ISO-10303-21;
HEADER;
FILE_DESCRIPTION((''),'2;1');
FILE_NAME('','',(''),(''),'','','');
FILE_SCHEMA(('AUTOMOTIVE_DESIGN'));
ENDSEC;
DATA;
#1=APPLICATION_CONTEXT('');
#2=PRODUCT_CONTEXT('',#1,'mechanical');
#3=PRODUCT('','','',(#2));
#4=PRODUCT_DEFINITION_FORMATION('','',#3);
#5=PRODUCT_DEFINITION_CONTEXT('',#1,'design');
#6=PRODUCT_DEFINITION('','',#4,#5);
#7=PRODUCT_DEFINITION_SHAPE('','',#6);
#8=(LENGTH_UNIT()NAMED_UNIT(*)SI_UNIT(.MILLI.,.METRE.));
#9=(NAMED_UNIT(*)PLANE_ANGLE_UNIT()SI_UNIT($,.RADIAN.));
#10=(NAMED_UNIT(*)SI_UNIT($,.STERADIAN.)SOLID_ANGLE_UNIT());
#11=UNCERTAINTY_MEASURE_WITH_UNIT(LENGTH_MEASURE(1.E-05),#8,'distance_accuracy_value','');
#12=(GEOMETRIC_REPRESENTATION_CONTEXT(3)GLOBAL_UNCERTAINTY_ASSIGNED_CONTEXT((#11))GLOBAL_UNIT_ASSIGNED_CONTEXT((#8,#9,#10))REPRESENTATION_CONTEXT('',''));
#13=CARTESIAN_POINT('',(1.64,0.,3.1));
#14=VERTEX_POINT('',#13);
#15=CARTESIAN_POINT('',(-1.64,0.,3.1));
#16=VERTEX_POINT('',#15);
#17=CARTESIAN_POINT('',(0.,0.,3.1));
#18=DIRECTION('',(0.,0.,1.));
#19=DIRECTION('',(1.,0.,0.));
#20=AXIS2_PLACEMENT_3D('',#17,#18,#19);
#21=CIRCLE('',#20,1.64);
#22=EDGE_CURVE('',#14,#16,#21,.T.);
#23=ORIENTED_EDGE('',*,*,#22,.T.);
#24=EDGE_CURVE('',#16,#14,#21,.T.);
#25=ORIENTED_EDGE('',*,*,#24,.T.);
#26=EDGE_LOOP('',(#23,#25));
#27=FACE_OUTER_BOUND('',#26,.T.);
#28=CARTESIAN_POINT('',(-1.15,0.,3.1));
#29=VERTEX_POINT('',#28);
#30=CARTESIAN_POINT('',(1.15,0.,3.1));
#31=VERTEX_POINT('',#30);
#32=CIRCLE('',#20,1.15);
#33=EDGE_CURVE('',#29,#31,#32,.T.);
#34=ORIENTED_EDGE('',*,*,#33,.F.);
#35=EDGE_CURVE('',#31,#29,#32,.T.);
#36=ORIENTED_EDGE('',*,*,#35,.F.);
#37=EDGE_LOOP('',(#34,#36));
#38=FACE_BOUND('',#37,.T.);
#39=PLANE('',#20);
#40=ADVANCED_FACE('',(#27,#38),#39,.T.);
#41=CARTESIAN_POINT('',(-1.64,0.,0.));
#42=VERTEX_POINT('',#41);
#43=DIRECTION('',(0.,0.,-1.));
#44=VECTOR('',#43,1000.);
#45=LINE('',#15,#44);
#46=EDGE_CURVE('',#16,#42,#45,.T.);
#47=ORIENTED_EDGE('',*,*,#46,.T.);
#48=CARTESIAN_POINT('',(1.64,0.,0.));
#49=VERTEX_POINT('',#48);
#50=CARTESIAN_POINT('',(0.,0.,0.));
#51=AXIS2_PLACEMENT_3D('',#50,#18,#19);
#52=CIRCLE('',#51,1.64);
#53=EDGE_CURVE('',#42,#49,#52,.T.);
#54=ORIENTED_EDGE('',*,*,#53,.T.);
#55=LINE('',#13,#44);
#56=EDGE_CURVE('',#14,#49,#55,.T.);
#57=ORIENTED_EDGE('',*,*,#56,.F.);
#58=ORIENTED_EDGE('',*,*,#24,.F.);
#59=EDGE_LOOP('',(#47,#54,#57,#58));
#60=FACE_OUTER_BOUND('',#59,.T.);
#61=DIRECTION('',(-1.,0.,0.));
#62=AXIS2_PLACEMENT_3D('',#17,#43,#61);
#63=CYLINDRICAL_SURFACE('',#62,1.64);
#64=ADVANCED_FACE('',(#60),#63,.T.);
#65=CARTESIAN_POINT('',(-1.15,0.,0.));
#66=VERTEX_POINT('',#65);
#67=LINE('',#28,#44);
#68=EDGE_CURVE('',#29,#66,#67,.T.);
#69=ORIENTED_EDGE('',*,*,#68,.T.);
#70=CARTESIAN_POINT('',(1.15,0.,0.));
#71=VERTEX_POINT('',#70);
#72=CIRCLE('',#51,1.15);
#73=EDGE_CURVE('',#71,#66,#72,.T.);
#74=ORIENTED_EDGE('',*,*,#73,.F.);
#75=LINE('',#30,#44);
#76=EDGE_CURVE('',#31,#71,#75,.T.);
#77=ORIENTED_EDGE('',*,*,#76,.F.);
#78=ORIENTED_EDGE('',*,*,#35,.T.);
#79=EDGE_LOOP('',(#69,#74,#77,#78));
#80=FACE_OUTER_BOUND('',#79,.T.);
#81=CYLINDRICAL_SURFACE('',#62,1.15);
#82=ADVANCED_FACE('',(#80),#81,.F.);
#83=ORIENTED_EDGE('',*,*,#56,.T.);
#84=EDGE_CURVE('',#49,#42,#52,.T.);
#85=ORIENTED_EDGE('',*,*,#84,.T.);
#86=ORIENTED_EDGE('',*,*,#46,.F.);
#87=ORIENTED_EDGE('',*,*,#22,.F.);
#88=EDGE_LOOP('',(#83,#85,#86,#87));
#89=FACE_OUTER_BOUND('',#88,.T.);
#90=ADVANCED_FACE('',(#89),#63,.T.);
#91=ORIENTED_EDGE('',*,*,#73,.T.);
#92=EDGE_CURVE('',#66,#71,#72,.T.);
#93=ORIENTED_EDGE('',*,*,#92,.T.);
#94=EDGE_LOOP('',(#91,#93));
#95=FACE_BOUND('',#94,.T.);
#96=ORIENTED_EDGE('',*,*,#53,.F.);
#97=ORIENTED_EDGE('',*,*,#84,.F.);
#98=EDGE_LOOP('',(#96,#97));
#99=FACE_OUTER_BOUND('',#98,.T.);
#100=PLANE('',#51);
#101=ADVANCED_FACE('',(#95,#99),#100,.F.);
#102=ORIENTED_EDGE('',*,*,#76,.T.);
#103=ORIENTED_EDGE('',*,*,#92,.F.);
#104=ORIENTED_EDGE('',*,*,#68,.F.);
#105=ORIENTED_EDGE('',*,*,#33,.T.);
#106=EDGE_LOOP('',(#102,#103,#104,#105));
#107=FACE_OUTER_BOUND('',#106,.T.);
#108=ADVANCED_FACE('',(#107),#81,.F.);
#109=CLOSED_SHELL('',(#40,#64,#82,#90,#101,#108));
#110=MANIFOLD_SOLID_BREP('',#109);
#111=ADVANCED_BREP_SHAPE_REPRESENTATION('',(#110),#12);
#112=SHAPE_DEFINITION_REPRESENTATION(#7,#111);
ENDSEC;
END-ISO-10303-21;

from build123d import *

# Parameters (mm, degrees)
SKETCH_1_R      = 1.64
SKETCH_1_R_2    = 1.15
EXTRUDE_1_DEPTH = 3.1


with BuildPart() as part:
    # 草图1 → 凸台-拉伸1 (new body)
    with BuildSketch(Plane.XY):
        with Locations(Location((0, 0, 0), (0, 0, 180))):
            Circle(SKETCH_1_R)
        with Locations(Location((0, 0, 0), (0, 0, 180))):
            Circle(SKETCH_1_R_2, mode=Mode.SUBTRACT)
    extrude(amount=EXTRUDE_1_DEPTH)


solid = part.part
